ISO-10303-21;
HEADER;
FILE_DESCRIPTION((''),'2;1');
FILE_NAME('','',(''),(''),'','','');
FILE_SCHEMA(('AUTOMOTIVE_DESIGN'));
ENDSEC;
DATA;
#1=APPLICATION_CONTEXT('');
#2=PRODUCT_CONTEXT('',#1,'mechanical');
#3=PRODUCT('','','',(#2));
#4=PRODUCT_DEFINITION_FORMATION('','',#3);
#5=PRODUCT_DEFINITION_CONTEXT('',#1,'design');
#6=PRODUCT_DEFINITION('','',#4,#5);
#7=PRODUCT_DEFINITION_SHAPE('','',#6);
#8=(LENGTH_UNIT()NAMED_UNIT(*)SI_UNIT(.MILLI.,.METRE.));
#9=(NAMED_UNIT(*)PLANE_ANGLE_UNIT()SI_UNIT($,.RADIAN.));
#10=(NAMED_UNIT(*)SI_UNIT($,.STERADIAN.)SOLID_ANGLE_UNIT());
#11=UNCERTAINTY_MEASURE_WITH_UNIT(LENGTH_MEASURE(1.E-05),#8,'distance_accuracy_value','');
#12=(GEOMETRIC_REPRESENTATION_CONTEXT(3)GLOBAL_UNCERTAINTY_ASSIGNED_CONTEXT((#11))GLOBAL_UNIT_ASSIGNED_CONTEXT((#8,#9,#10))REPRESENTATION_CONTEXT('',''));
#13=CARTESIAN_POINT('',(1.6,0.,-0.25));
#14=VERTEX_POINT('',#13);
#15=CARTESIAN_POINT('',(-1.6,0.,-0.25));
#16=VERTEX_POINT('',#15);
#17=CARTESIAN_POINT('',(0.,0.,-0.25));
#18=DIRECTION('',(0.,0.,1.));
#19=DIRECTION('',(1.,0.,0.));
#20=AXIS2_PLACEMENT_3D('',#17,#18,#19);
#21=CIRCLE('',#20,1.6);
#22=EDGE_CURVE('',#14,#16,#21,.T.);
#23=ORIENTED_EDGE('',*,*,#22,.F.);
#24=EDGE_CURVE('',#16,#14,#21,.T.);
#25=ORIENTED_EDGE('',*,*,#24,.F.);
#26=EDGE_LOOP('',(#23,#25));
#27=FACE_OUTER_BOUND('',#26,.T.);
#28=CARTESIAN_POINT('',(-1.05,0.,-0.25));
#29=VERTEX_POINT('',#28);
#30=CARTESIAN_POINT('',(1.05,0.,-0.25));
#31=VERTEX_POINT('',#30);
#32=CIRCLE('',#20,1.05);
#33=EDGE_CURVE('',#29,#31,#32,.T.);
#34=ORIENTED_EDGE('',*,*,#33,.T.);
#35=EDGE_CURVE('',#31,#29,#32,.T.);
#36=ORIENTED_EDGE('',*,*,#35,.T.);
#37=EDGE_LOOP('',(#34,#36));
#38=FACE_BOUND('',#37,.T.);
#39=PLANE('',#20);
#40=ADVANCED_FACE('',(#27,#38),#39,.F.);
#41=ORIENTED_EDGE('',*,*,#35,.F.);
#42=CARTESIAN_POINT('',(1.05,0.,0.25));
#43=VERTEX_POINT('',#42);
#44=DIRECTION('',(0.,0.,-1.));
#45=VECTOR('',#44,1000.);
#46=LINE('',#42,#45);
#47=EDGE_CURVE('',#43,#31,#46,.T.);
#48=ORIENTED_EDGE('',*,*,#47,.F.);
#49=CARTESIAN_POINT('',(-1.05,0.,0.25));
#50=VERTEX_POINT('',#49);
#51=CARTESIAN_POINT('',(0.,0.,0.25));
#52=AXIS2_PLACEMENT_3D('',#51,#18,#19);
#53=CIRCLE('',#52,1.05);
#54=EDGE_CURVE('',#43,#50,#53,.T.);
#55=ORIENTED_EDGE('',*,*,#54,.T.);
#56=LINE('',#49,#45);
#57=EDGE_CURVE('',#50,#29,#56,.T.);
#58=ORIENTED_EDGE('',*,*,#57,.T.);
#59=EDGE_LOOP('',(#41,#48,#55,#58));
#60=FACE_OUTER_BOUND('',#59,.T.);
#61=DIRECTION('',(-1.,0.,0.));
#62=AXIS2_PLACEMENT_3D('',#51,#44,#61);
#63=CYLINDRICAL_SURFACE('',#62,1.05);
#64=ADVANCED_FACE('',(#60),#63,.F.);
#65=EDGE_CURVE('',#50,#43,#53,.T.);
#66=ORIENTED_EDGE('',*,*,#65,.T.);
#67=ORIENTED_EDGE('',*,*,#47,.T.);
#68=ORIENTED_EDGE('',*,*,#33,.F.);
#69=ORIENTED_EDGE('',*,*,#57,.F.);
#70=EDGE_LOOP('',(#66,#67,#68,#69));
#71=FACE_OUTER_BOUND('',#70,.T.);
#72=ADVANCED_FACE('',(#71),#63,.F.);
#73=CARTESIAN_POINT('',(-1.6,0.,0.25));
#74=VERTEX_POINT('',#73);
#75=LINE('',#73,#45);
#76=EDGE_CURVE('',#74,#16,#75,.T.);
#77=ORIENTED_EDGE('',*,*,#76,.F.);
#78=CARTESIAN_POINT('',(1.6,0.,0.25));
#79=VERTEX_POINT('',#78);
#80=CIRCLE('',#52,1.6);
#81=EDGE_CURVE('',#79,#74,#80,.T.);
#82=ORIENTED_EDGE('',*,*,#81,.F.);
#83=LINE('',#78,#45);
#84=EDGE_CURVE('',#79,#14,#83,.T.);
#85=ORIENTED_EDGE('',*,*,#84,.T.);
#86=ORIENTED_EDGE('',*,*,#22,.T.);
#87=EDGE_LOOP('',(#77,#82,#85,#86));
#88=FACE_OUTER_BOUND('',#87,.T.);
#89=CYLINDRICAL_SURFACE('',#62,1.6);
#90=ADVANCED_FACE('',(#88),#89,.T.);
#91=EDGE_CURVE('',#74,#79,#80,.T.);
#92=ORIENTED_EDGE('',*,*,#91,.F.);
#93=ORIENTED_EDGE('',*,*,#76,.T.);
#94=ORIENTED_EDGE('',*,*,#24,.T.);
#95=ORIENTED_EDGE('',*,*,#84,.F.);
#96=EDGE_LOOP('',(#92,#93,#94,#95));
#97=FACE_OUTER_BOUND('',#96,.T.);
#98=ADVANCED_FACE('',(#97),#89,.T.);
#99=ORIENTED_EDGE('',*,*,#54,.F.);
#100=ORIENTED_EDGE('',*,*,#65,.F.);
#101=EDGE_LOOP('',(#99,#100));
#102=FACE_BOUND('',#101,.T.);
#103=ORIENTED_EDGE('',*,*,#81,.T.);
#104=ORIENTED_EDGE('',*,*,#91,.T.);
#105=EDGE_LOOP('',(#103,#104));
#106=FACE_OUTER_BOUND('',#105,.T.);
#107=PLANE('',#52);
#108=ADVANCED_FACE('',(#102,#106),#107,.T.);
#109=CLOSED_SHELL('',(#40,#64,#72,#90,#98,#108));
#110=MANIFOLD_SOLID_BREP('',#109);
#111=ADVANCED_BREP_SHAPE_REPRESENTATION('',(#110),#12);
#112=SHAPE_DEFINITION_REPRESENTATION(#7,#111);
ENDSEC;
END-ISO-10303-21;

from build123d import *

# Parameters (mm, degrees)
SKETCH1_R           = 1.6
SKETCH1_R_2         = 1.05
BOSS_EXTRUDE1_DEPTH = 0.25


with BuildPart() as part:
    # Sketch1 → Boss-Extrude1 (new, symmetric)
    with BuildSketch(Plane.XY):
        Circle(SKETCH1_R)
        Circle(SKETCH1_R_2, mode=Mode.SUBTRACT)
    extrude(amount=BOSS_EXTRUDE1_DEPTH, both=True)


solid = part.part
